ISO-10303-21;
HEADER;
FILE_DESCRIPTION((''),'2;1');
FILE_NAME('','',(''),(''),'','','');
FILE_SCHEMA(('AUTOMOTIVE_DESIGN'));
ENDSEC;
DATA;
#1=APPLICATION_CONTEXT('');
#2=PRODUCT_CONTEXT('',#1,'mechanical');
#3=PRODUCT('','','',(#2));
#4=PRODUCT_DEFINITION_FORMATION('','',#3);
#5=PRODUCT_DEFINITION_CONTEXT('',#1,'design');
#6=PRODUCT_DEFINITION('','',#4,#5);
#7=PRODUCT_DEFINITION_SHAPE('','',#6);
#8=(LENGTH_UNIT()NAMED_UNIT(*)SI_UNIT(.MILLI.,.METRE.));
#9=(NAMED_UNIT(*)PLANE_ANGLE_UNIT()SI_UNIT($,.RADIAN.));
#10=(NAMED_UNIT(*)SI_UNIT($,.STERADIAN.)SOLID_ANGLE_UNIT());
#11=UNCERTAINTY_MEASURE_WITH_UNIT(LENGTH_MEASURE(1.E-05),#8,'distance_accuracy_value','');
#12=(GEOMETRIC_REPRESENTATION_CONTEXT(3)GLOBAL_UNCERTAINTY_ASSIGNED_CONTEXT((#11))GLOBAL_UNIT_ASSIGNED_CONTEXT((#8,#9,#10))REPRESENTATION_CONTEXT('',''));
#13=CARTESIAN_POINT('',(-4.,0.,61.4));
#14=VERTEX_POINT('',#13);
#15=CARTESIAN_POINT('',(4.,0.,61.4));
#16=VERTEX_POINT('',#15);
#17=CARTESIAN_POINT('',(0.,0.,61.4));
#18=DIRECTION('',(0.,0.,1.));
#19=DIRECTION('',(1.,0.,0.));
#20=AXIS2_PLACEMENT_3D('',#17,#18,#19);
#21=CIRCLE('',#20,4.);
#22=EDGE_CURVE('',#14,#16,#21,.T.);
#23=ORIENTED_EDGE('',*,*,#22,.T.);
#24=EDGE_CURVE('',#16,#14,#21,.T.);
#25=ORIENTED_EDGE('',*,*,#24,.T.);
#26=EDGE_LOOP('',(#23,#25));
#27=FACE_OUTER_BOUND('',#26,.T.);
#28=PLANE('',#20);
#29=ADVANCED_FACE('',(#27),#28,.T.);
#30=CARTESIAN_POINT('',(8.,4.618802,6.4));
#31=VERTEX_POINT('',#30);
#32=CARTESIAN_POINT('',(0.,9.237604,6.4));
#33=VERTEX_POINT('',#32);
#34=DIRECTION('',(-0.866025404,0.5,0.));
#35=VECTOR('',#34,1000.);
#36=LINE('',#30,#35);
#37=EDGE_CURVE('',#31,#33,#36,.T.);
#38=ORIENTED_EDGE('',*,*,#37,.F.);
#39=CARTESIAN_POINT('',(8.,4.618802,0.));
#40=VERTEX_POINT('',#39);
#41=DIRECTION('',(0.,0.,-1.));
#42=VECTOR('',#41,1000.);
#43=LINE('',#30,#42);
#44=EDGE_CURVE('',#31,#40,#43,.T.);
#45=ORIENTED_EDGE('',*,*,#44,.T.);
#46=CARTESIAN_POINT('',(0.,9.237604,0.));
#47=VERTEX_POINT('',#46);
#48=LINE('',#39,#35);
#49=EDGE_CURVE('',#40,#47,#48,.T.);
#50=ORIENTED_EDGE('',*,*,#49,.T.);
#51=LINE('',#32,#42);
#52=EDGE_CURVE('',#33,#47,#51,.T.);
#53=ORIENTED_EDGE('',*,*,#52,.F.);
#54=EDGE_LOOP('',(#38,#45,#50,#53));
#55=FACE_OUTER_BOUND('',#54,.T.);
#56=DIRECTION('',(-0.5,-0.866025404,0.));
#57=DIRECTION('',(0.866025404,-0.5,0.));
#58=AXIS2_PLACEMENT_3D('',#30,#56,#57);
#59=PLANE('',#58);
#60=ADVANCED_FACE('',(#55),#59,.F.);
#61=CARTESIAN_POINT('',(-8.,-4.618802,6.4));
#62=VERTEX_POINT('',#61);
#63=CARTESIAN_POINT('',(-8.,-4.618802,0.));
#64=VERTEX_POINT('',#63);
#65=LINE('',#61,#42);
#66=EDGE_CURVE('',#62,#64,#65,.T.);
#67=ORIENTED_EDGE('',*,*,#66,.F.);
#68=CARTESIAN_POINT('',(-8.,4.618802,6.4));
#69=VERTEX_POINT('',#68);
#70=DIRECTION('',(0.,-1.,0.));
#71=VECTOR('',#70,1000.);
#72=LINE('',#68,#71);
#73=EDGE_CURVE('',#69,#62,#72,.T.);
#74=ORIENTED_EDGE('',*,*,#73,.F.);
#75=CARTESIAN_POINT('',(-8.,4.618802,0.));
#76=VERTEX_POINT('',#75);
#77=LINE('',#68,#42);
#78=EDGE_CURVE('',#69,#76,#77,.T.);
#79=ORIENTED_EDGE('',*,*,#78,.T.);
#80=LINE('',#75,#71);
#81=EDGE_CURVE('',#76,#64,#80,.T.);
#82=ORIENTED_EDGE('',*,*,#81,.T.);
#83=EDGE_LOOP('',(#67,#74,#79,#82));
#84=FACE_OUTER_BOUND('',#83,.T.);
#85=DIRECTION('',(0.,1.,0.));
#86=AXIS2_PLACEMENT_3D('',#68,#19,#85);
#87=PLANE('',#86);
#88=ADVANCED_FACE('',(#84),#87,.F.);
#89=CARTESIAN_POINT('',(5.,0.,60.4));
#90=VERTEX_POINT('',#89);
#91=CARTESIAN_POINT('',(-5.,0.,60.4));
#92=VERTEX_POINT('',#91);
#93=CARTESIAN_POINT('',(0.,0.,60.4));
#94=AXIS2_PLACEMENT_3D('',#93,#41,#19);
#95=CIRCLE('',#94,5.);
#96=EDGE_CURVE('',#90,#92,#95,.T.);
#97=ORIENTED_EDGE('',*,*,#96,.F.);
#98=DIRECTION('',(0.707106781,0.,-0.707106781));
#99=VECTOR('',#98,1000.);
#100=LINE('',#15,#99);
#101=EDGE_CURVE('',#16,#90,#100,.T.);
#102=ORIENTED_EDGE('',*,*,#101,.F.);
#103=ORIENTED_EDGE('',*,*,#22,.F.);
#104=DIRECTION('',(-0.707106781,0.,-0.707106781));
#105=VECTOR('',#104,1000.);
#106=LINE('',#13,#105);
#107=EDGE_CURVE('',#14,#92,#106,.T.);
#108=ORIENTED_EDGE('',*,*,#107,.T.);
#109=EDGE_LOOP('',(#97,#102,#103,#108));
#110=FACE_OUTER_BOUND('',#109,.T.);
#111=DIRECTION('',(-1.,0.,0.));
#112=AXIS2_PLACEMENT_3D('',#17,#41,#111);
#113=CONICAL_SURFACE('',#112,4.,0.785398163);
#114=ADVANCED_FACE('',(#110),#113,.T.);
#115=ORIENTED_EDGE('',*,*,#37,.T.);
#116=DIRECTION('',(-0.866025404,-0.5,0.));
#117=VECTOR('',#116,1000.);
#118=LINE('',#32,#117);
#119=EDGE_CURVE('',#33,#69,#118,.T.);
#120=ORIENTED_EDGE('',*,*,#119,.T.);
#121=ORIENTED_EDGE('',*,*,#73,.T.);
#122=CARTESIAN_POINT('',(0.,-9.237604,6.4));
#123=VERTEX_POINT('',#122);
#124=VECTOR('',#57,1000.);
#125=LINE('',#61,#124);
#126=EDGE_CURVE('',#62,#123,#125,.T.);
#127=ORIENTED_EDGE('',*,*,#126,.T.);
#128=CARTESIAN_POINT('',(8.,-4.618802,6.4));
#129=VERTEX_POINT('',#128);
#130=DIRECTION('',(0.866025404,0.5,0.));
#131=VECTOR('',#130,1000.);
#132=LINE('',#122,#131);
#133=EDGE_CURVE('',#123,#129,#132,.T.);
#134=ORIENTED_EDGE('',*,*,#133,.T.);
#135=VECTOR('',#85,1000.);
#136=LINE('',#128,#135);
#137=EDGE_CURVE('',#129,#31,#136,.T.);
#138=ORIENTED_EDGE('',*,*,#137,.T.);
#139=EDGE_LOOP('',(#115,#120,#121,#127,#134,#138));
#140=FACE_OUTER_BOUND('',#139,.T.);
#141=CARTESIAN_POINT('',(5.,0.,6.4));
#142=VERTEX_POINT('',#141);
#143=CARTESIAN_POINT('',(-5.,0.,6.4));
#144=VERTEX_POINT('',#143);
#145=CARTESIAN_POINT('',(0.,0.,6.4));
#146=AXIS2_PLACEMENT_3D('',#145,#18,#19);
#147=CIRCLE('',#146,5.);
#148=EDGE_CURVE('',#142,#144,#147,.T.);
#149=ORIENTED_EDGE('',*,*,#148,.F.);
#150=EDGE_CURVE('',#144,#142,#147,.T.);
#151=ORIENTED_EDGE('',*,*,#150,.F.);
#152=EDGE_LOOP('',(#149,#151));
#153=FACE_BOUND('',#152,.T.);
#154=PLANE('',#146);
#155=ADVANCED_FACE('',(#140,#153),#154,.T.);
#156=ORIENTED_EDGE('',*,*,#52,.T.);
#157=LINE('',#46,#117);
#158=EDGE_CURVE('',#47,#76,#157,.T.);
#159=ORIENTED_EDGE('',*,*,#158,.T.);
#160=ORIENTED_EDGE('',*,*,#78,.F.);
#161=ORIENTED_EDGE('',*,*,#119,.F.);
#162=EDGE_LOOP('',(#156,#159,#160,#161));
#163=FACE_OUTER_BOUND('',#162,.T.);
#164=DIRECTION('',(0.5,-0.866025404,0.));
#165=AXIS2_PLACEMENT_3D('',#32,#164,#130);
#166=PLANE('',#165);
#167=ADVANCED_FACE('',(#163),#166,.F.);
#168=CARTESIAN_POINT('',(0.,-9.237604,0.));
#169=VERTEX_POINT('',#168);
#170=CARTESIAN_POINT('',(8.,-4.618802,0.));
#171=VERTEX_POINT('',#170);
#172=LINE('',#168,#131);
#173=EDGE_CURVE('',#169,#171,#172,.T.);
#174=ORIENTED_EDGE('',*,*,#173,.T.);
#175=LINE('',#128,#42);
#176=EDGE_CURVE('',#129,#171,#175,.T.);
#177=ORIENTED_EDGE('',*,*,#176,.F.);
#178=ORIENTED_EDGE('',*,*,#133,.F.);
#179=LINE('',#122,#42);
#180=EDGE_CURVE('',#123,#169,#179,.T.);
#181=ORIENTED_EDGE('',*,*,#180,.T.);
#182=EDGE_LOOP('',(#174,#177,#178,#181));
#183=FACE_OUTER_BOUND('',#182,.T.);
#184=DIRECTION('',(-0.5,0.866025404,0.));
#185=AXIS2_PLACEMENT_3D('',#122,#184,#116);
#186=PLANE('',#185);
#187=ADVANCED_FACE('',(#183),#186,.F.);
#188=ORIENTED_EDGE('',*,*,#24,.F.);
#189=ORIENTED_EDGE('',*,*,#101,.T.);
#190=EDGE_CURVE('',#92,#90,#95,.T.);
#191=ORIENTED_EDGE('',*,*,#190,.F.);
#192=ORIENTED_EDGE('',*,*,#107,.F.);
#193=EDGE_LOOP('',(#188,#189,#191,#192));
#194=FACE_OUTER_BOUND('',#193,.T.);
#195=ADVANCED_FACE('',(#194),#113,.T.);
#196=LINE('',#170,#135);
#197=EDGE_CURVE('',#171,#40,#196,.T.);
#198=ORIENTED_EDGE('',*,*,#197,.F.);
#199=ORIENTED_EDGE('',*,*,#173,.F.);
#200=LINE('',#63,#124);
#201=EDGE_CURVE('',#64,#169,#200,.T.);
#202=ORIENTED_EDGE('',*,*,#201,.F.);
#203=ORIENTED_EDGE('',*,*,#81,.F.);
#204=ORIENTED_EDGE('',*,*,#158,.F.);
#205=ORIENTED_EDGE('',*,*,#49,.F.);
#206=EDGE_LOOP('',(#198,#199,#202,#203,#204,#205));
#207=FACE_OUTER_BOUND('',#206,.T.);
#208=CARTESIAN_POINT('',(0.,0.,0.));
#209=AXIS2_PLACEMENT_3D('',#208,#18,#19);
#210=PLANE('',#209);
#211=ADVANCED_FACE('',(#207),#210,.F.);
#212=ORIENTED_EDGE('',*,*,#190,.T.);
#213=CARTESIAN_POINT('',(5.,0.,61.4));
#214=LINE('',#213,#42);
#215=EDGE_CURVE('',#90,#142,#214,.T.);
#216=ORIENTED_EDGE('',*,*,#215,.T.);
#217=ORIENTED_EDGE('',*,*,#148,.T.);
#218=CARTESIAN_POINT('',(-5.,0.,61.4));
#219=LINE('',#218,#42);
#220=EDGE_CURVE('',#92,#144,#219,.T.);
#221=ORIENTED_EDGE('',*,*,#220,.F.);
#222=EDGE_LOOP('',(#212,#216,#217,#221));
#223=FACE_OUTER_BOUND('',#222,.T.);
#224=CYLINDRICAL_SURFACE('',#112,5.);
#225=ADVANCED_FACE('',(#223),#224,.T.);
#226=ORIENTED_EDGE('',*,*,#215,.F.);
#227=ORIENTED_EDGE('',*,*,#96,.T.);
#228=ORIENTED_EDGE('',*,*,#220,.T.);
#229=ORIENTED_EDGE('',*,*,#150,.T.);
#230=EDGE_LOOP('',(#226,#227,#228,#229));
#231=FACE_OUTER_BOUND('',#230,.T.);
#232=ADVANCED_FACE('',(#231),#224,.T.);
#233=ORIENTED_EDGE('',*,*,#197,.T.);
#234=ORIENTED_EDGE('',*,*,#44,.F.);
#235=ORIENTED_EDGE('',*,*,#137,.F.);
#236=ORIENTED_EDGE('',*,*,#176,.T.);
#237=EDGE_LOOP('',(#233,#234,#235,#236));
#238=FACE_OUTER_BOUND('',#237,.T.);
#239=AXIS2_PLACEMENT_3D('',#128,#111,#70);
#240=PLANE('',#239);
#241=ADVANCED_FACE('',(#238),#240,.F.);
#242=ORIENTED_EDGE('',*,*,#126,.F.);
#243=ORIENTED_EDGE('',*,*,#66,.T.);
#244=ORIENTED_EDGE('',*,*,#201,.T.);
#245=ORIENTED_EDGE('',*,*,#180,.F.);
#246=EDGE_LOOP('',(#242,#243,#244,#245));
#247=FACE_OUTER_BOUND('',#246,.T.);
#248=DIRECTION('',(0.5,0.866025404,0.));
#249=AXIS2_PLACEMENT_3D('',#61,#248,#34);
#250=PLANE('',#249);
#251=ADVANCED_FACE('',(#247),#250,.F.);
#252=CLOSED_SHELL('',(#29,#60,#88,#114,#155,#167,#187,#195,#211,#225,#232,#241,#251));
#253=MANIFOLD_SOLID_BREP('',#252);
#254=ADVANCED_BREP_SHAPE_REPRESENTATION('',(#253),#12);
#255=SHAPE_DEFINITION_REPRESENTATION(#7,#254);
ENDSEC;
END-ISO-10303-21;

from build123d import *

# Parameters (mm, degrees)
BOSS_EXTRUDE1_DEPTH = 6.4
SKETCH3_R           = 5
BOSS_EXTRUDE2_DEPTH = 55
CHAMFER1_SIZE       = 1


with BuildPart() as part:
    # Sketch1 → Boss-Extrude1 (new body)
    with BuildSketch(Plane.XY):
        Polygon((8, 4.618802154), (0, 9.237604307), (-8, 4.618802154), (-8, -4.618802154), (0, -9.237604307), (8, -4.618802154), align=None)
    extrude(amount=BOSS_EXTRUDE1_DEPTH)

    # Sketch3 → Boss-Extrude2 (add)
    with BuildSketch(Plane.XY.offset(6.4)):
        Circle(SKETCH3_R)
    extrude(amount=BOSS_EXTRUDE2_DEPTH)

    # Chamfer1
    chamfer1_edges = [part.edges().sort_by_distance(p)[0] for p in [
        (-5, 0, 61.4),
    ]]
    chamfer(chamfer1_edges, length=CHAMFER1_SIZE)


solid = part.part
